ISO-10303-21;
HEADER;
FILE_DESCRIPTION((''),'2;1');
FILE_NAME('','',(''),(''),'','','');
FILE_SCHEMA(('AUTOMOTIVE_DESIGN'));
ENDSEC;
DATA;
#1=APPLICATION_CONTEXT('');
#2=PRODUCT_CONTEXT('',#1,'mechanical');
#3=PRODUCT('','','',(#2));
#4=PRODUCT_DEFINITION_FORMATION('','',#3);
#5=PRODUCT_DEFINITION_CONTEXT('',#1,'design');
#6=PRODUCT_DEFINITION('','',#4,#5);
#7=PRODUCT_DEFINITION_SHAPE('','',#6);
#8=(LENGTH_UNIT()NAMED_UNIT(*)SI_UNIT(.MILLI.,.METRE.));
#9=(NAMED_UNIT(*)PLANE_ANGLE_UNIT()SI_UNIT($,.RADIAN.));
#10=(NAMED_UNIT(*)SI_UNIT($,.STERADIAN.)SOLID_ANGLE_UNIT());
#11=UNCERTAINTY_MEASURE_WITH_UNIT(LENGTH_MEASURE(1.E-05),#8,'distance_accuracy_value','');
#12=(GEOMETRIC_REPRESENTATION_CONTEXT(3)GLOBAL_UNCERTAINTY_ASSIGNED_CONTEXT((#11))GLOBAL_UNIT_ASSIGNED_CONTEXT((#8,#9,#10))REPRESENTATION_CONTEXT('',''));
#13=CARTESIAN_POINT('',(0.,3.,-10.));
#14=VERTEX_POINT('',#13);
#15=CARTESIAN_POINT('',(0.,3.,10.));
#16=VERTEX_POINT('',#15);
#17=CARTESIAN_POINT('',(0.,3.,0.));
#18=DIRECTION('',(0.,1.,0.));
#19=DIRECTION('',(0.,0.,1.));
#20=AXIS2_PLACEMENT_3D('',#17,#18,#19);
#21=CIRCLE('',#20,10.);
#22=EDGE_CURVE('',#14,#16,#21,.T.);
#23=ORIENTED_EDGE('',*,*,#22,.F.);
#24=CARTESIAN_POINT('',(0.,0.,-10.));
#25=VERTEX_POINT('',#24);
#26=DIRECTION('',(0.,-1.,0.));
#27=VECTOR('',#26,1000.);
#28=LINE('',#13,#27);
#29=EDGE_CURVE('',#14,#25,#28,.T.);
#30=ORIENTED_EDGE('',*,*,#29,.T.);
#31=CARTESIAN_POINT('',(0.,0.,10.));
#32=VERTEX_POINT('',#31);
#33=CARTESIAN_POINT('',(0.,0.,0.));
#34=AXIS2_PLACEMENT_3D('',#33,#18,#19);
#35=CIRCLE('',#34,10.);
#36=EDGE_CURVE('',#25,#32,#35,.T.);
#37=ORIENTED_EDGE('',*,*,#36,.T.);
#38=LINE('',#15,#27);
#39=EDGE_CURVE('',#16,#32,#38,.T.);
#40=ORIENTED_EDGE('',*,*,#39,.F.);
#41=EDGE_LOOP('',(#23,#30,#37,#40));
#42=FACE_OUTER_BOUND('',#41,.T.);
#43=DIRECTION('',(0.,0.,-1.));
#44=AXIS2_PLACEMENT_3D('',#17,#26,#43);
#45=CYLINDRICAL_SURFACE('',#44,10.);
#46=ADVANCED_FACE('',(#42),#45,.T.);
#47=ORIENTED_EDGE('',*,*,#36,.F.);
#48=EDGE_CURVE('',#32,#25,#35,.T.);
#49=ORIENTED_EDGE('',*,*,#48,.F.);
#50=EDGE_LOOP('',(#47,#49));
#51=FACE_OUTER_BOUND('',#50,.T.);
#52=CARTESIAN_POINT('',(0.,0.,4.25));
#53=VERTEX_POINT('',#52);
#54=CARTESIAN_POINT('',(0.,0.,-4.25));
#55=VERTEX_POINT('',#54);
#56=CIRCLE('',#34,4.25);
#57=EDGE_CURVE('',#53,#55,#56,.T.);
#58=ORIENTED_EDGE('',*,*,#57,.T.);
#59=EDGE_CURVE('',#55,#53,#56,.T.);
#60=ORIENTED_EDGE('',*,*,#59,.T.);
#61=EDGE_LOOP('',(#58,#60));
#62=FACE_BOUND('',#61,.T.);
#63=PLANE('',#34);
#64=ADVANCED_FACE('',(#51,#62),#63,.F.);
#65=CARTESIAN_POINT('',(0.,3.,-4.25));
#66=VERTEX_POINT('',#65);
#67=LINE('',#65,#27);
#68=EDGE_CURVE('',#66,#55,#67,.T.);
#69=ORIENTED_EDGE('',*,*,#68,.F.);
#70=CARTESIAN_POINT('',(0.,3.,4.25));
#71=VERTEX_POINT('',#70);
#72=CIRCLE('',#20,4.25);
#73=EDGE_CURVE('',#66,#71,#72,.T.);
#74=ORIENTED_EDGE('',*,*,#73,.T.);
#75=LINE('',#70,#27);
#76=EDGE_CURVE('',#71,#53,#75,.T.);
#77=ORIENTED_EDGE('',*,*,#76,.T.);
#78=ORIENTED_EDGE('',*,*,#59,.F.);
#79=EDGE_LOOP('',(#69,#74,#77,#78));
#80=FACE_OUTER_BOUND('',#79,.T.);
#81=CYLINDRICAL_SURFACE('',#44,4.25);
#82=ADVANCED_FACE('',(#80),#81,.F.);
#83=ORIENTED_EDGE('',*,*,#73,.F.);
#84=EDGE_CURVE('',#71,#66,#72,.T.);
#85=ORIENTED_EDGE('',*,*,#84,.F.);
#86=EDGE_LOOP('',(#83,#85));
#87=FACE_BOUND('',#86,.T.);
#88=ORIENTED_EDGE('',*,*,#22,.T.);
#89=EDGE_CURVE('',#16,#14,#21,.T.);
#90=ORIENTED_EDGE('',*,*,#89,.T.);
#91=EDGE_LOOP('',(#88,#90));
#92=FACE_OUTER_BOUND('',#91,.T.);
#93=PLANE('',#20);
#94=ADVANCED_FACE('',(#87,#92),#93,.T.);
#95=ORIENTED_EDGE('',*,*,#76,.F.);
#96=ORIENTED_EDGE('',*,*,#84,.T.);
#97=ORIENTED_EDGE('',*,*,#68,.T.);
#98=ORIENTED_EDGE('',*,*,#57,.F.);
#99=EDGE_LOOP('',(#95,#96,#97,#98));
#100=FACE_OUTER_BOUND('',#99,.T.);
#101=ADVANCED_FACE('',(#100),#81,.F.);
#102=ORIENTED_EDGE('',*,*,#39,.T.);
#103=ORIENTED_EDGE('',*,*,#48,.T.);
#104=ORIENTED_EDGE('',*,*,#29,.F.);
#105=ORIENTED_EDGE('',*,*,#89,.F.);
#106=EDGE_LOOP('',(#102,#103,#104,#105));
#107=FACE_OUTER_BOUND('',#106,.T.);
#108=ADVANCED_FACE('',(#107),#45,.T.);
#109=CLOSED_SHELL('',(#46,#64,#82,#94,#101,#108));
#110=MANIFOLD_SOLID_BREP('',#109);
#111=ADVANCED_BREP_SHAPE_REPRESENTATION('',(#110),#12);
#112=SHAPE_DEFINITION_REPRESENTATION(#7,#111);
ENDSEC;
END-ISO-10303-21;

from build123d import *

# Parameters (mm, degrees)
SKETCH1_R           = 10
SKETCH1_R_2         = 4.25
BOSS_EXTRUDE1_DEPTH = 3


with BuildPart() as part:
    # Sketch1 → Boss-Extrude1 (new body)
    with BuildSketch(Plane(origin=(0, 0, 0), x_dir=(1, 0, 0), z_dir=(0, 1, 0))):
        with Locations(Location((0, 0, 0), (0, 0, 270))):
            Circle(SKETCH1_R)
        with Locations(Location((0, 0, 0), (0, 0, 270))):
            Circle(SKETCH1_R_2, mode=Mode.SUBTRACT)
    extrude(amount=BOSS_EXTRUDE1_DEPTH)


solid = part.part
